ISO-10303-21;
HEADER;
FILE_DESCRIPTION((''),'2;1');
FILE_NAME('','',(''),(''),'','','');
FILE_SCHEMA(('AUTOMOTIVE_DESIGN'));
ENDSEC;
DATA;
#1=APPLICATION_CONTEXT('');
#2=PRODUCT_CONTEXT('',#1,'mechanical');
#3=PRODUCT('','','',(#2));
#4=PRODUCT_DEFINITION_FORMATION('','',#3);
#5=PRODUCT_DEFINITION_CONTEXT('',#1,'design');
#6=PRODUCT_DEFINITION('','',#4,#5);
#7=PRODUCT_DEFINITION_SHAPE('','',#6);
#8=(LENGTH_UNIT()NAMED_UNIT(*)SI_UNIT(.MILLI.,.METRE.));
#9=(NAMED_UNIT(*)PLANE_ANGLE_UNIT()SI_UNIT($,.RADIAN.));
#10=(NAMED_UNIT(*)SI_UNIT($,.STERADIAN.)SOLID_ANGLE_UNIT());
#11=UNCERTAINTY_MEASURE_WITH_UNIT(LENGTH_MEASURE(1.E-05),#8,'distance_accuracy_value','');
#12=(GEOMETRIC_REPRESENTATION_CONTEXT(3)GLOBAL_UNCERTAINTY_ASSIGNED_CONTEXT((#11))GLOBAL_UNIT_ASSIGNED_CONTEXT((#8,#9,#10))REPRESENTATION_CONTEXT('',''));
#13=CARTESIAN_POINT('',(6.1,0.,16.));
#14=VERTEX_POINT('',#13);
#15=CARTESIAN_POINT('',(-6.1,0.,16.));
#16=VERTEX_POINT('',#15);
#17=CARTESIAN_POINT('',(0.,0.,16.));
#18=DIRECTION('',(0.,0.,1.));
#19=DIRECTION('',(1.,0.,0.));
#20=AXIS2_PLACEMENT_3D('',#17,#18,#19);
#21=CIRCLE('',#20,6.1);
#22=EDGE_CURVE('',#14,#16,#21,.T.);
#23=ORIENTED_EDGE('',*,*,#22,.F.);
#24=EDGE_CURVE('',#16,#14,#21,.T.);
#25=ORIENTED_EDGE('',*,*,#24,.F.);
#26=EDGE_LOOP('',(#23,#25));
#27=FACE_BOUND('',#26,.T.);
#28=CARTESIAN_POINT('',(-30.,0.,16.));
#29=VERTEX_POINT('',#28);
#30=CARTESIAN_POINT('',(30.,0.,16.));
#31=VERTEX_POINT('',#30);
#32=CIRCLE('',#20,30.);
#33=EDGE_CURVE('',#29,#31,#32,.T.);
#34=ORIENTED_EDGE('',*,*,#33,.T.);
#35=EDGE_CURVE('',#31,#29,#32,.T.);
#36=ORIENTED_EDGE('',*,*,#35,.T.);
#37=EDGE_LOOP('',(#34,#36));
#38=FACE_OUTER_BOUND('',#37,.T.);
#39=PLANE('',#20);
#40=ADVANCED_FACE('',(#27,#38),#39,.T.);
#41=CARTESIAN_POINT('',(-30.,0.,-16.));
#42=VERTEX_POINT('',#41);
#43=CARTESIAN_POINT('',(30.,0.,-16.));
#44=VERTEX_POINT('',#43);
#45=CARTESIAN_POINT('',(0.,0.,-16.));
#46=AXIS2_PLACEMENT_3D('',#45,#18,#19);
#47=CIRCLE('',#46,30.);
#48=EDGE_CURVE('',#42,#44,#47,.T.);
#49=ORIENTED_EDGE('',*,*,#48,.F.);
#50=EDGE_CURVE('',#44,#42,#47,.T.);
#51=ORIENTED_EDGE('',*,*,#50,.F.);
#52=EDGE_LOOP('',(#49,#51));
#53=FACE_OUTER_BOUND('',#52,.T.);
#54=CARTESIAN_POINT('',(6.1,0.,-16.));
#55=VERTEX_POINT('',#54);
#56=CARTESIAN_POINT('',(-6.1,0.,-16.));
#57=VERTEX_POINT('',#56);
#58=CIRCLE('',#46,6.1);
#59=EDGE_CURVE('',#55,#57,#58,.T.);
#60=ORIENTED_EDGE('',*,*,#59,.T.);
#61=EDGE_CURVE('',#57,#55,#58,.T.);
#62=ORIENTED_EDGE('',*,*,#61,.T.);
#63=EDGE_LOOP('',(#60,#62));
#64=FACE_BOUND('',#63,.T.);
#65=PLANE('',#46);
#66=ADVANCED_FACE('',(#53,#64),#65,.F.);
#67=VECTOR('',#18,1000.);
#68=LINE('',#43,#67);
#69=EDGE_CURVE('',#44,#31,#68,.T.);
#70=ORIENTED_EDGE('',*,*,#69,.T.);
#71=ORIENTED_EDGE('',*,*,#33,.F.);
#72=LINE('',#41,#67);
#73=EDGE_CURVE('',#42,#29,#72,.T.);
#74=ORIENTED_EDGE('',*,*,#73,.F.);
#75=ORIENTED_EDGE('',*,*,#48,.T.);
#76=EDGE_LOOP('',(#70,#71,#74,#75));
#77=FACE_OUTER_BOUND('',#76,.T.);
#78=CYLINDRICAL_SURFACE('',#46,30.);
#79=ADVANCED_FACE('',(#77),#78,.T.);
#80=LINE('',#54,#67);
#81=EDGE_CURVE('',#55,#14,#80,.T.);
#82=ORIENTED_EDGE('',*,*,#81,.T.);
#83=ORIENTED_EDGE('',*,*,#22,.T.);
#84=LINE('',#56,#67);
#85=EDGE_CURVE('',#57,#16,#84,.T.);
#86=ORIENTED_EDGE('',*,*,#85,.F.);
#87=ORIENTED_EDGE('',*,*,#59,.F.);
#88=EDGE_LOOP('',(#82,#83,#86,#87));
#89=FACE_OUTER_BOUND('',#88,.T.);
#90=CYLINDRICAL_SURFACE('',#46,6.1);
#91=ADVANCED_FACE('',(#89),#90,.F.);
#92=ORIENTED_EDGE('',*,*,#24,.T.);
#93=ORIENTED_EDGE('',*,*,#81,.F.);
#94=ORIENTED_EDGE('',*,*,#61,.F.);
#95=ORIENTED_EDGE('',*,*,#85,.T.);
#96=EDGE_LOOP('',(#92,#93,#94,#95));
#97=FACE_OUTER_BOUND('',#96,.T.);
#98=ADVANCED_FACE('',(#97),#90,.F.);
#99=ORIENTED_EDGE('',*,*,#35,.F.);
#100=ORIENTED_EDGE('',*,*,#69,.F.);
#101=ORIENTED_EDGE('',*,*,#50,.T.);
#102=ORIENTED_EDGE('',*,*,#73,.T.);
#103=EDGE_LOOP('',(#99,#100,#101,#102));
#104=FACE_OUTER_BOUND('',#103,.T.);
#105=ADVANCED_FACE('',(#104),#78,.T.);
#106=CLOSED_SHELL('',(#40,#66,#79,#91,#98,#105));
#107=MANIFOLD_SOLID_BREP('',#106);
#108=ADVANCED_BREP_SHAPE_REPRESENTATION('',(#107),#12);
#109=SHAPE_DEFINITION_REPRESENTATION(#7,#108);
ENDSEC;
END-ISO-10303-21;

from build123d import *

# Parameters (mm, degrees)
SKETCH_1_R      = 30
SKETCH_1_R_2    = 6.1
EXTRUDE_1_DEPTH = 16


with BuildPart() as part:
    # 草图1 → 凸台-拉伸1 (new, symmetric)
    with BuildSketch(Plane.XY):
        Circle(SKETCH_1_R)
        Circle(SKETCH_1_R_2, mode=Mode.SUBTRACT)
    extrude(amount=EXTRUDE_1_DEPTH, both=True)


solid = part.part
